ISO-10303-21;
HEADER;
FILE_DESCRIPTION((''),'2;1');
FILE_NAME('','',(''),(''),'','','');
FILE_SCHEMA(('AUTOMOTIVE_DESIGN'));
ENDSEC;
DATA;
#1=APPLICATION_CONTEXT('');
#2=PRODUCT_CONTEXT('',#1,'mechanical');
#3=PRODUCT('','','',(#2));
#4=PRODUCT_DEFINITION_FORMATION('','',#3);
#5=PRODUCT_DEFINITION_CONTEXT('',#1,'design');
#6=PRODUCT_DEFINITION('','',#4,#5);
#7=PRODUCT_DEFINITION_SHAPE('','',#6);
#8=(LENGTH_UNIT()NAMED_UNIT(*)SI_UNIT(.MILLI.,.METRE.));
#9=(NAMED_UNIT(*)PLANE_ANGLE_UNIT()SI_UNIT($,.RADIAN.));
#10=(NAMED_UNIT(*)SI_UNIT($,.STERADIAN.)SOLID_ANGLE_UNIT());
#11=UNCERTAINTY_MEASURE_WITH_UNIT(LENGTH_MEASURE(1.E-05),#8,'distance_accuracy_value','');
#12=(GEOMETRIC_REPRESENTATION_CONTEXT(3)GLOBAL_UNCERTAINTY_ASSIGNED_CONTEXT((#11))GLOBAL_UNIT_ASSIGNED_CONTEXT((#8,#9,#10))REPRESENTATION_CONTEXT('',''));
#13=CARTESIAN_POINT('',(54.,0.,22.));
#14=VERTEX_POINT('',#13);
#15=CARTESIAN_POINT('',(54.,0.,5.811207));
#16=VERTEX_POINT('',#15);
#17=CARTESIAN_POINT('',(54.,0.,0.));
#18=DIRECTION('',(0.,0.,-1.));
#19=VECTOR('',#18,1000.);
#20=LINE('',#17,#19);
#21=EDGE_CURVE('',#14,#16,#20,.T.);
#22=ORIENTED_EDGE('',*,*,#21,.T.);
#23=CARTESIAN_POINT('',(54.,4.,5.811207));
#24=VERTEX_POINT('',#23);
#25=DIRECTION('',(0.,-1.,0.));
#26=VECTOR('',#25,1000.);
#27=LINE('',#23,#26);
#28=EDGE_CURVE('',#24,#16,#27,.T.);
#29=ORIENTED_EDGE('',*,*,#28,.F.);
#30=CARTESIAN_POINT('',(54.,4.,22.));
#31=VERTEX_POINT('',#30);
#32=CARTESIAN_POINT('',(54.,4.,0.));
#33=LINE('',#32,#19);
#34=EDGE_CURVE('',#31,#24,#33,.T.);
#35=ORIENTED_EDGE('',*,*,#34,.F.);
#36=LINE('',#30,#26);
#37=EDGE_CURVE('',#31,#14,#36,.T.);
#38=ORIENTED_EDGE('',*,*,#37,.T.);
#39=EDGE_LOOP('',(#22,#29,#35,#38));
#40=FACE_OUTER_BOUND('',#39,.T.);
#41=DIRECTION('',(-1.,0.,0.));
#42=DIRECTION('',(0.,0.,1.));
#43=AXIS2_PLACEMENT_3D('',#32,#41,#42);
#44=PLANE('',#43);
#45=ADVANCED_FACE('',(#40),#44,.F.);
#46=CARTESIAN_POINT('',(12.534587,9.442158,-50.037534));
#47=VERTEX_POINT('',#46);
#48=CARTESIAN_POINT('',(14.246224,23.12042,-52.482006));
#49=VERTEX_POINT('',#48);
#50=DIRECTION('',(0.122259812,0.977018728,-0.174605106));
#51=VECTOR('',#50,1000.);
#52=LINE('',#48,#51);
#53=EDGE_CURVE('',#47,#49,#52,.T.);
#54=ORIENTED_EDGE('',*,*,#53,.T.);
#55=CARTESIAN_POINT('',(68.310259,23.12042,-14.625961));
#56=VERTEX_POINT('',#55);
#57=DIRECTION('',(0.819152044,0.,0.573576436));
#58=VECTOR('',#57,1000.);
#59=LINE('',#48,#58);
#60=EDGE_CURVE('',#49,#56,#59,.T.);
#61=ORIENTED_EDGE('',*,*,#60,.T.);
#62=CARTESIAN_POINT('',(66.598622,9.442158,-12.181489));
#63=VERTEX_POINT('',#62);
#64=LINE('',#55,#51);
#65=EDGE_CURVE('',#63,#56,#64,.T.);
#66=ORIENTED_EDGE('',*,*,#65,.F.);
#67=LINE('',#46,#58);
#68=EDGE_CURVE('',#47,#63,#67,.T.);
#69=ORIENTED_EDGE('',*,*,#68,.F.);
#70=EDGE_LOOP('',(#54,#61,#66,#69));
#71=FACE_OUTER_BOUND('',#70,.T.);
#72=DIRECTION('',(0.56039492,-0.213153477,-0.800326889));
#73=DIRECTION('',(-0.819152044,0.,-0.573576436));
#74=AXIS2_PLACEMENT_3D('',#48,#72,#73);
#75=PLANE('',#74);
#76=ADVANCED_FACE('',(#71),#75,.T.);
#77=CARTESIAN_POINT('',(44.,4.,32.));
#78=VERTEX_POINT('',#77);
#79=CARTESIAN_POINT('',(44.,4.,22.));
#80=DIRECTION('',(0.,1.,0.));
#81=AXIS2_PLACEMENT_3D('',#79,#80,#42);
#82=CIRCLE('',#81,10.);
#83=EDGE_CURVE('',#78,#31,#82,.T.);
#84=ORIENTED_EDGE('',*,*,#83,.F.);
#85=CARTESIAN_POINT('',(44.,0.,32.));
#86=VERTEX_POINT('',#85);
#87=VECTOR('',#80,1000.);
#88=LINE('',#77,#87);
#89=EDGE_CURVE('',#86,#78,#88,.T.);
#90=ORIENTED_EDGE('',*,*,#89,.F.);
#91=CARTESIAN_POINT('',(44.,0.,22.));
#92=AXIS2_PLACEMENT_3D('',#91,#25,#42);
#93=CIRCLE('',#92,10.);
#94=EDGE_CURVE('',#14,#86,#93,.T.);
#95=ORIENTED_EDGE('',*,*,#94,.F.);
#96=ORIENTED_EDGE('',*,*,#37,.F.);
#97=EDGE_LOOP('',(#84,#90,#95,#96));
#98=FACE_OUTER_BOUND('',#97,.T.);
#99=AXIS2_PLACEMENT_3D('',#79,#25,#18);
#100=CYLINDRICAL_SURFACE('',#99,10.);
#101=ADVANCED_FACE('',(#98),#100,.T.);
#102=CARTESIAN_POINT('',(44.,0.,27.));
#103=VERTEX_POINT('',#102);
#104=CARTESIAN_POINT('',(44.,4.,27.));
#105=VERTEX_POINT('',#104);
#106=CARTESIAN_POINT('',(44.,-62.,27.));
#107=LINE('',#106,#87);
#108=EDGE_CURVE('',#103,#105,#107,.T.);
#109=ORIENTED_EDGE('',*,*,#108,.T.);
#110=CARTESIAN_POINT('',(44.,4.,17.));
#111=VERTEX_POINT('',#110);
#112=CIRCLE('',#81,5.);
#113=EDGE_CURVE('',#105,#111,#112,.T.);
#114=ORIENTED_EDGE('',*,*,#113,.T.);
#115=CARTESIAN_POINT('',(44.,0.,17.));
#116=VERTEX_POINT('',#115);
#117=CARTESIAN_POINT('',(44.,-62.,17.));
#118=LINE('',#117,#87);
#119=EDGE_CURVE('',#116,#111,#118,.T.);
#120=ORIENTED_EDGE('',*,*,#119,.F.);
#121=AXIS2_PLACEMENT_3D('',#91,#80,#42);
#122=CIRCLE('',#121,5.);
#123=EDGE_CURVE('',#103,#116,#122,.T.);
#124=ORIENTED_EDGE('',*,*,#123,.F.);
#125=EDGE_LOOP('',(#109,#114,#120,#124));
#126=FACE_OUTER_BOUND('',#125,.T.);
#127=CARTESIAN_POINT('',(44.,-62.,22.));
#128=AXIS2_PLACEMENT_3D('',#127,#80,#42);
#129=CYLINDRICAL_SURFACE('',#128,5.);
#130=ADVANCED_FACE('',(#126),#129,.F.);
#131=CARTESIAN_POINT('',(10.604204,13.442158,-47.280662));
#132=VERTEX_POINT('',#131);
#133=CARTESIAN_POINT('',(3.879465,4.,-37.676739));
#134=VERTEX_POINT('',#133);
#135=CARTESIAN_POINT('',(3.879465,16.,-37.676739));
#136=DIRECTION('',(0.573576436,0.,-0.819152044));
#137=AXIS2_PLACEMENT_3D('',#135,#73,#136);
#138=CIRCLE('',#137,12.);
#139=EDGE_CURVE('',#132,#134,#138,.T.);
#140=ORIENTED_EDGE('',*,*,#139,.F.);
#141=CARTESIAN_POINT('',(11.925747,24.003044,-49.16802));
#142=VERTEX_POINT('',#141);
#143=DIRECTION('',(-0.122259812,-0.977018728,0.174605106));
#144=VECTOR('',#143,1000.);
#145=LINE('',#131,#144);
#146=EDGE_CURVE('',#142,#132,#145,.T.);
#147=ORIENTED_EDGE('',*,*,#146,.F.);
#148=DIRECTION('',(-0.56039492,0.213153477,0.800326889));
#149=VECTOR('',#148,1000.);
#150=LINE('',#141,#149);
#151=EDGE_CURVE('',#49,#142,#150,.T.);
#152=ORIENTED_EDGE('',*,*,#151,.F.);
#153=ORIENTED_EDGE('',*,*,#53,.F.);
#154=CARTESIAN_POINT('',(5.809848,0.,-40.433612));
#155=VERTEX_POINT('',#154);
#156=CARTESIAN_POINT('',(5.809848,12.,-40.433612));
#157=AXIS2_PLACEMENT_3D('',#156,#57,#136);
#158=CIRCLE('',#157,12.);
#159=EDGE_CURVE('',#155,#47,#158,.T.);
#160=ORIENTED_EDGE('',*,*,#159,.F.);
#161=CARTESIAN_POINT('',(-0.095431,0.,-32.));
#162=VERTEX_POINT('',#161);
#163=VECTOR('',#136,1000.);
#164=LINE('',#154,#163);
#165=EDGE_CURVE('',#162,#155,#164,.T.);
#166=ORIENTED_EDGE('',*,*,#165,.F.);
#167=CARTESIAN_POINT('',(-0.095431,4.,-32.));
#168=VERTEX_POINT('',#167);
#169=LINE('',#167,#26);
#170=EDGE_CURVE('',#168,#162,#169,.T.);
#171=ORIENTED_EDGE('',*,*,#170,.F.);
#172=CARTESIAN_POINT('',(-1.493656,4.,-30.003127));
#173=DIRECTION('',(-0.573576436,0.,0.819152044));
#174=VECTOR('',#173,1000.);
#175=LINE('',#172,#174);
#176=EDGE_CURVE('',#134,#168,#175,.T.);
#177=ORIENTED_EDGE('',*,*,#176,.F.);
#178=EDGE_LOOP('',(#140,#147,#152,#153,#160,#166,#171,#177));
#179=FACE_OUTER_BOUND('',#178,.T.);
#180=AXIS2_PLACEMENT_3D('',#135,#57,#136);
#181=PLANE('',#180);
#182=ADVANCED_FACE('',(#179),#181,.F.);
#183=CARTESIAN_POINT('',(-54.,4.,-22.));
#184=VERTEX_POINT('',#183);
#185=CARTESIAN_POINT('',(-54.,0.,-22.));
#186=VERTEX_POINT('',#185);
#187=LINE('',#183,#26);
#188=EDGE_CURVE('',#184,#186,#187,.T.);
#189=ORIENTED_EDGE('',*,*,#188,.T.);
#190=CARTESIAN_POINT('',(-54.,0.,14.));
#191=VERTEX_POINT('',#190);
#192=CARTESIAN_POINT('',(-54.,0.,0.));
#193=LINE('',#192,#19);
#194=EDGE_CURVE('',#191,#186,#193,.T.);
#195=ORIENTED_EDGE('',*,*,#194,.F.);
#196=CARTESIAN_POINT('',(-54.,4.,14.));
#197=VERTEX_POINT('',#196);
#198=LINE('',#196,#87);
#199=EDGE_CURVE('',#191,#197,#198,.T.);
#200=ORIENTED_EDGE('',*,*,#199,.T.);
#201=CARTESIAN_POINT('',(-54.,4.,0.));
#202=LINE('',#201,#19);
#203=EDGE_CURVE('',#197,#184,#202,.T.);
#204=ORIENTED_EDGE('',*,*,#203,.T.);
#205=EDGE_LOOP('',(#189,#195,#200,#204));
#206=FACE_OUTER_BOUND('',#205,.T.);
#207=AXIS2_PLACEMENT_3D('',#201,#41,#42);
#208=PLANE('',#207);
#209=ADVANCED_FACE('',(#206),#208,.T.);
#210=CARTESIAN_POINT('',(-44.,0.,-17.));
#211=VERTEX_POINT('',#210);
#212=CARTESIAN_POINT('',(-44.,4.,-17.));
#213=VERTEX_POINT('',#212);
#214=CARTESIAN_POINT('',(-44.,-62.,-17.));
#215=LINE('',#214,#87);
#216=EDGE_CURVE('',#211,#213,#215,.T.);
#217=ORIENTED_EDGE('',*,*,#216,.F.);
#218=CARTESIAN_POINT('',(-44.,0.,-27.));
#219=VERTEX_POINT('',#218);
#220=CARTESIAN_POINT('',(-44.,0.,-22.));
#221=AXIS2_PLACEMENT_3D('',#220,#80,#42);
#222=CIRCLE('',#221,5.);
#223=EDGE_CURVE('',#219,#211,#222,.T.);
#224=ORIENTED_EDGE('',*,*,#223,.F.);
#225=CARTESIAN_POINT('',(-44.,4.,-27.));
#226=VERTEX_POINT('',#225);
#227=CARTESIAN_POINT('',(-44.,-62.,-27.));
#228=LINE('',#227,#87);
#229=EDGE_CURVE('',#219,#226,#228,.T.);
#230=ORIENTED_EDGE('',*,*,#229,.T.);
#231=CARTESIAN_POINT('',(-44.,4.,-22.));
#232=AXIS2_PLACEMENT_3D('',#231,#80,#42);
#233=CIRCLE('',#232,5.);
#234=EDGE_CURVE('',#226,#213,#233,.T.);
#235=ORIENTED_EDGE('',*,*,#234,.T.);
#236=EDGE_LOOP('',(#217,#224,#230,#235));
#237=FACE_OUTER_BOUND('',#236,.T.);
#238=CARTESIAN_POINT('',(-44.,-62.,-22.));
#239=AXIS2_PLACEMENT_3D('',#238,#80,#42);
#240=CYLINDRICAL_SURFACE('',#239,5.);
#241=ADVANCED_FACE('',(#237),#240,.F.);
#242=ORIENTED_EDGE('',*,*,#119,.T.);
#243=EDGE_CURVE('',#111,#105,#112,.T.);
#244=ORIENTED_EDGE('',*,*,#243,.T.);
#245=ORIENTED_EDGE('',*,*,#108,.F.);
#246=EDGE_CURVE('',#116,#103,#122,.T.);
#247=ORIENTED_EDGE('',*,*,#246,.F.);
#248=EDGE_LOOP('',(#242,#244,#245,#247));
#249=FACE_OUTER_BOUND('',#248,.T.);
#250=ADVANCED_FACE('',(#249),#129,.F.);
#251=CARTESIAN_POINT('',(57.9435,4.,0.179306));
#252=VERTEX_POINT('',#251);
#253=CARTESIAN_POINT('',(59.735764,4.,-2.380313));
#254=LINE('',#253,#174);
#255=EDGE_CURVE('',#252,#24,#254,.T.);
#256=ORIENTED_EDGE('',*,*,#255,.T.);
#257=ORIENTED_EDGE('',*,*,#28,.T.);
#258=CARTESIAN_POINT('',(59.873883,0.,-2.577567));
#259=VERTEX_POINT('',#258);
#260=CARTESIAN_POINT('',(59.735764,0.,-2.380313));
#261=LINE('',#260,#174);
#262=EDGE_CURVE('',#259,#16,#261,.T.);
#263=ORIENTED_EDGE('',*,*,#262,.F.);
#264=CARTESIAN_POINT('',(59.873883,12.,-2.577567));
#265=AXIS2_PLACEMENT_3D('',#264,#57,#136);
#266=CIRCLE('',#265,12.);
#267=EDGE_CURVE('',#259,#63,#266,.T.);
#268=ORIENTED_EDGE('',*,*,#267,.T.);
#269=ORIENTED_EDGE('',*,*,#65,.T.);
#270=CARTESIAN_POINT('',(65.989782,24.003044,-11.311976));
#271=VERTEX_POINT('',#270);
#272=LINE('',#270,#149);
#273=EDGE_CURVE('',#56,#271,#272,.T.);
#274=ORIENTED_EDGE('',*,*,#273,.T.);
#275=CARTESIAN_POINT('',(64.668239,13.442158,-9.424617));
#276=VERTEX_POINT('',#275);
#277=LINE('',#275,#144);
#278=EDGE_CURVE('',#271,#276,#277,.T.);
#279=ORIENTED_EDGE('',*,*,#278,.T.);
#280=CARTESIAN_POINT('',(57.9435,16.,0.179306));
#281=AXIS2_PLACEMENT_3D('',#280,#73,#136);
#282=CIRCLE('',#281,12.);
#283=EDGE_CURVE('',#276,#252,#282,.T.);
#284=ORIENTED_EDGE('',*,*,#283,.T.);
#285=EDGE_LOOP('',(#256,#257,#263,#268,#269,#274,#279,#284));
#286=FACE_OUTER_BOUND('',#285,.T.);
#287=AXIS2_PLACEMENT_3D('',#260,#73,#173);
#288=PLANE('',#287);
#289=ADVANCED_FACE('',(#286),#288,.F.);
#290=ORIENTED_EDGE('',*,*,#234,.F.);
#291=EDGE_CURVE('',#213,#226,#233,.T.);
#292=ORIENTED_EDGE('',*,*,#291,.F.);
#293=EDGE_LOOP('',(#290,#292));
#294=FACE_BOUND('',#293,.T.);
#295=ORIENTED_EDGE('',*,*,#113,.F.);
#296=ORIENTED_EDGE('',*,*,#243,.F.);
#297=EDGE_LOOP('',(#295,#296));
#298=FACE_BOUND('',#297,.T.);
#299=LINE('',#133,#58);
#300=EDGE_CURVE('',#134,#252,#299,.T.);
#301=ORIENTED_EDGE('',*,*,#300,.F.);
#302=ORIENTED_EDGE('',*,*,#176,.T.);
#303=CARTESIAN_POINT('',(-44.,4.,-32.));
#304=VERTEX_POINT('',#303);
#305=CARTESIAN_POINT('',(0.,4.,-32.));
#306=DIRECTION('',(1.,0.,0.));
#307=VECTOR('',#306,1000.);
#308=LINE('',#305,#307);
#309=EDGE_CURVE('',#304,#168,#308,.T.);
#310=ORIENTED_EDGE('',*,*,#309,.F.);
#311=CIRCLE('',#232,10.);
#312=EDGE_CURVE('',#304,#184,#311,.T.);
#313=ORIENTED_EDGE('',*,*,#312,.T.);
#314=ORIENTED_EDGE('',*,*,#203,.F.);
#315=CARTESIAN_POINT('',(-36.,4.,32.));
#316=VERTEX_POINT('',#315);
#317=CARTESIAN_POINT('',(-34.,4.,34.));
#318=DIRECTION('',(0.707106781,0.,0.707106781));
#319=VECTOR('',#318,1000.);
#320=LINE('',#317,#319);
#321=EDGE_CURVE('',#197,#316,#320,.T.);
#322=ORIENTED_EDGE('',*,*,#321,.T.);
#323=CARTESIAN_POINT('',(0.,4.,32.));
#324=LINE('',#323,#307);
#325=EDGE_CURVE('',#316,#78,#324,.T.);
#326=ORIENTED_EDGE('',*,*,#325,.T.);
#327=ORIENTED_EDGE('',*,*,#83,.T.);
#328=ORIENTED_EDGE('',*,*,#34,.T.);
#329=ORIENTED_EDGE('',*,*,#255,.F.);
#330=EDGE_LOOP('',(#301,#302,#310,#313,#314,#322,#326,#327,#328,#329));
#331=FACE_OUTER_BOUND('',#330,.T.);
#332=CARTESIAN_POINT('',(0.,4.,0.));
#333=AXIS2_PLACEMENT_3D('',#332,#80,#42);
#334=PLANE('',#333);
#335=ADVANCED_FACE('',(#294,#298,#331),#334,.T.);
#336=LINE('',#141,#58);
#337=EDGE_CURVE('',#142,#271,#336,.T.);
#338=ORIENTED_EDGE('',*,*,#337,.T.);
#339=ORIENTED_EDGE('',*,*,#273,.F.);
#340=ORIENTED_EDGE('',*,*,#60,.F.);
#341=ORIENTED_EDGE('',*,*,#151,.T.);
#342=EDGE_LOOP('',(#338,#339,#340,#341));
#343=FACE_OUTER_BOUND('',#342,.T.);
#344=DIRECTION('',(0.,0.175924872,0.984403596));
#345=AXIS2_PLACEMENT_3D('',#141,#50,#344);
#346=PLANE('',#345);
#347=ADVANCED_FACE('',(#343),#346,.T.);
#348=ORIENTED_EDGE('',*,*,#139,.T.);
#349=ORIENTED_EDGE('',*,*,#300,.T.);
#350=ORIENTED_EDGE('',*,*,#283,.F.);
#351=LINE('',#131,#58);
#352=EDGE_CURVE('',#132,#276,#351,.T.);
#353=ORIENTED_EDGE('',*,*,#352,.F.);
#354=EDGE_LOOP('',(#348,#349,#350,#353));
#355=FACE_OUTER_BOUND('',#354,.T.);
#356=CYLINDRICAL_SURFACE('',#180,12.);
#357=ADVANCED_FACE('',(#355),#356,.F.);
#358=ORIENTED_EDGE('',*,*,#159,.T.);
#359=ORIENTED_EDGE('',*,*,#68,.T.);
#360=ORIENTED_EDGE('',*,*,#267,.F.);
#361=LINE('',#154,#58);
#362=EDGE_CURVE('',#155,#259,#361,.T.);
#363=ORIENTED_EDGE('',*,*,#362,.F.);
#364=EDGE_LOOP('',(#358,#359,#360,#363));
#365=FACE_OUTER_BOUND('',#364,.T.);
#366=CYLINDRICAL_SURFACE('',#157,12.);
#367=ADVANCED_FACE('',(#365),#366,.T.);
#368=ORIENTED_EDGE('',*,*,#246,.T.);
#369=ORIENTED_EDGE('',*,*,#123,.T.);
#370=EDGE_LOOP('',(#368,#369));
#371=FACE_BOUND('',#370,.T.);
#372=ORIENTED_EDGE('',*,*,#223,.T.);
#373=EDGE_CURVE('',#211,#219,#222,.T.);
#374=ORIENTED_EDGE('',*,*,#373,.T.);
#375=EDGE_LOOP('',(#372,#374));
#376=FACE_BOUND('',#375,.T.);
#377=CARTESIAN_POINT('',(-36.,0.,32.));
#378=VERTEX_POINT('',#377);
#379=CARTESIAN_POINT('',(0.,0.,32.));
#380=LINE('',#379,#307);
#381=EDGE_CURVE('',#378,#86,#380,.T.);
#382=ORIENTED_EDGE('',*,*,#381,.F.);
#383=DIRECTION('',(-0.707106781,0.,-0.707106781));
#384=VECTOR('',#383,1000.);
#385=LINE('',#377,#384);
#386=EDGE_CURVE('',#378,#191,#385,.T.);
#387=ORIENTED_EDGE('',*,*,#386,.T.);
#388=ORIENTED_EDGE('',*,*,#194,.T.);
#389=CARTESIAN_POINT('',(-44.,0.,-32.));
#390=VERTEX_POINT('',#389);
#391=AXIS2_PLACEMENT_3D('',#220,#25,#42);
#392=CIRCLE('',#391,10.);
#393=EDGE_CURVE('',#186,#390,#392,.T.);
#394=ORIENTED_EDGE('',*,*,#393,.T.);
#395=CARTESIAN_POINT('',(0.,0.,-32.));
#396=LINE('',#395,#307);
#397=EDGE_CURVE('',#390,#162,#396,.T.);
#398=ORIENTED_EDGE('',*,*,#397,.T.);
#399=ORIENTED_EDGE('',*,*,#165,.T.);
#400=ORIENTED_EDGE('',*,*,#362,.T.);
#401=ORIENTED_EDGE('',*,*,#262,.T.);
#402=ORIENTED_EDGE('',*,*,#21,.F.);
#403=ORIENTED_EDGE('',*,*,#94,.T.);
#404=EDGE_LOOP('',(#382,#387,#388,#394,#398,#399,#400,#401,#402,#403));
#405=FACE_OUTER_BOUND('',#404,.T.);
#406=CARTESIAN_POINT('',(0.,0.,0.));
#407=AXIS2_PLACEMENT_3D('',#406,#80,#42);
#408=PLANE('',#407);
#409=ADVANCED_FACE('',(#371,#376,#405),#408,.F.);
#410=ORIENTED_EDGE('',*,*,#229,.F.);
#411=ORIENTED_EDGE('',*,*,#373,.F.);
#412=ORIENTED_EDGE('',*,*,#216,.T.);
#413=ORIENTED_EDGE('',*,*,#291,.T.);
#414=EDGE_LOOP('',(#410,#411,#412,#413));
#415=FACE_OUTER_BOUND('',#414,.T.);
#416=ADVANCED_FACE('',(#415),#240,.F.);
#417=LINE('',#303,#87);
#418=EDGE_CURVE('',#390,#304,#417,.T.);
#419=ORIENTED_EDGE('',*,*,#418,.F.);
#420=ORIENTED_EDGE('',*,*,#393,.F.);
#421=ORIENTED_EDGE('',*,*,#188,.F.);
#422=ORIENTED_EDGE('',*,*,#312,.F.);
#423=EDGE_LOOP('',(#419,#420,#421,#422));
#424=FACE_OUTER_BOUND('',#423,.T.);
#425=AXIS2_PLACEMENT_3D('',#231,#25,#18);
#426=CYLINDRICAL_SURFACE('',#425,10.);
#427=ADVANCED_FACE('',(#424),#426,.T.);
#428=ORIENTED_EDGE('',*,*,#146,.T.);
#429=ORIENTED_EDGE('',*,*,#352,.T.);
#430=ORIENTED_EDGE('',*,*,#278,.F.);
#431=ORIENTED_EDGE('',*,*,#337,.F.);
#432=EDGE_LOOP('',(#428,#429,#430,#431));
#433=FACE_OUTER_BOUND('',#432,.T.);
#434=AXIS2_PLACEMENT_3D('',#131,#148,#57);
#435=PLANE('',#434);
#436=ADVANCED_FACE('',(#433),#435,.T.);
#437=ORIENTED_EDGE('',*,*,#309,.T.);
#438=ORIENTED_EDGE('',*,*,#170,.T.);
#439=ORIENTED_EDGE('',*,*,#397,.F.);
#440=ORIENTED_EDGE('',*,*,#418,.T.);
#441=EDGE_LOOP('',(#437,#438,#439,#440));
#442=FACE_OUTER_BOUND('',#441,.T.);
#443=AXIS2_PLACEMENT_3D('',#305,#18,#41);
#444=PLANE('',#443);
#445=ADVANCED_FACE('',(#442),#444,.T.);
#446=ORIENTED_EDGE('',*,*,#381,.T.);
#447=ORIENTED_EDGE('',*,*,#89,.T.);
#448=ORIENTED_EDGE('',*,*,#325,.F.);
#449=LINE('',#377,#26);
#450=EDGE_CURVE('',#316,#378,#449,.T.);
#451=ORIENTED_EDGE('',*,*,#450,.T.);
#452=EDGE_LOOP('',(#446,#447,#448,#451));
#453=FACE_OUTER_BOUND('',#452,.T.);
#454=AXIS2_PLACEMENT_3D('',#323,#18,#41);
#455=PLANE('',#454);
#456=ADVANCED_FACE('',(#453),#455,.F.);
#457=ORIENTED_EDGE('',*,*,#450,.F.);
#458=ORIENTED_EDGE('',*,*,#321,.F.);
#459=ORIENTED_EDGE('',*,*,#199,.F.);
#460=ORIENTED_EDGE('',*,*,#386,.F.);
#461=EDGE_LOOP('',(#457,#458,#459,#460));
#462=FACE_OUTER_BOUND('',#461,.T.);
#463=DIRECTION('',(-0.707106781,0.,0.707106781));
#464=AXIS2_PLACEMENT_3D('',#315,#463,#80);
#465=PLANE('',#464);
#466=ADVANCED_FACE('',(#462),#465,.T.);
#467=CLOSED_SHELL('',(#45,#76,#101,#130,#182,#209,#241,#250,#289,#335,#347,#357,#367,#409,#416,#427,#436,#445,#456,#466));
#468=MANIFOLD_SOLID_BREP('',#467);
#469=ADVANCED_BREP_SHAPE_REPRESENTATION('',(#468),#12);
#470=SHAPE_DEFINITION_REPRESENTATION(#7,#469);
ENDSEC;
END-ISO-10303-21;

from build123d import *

# Parameters (mm, degrees)
BASE_PLATE_DEPTH             = 4
FLANGE_RISER_SKETCH_W        = 65.921827793
FLANGE_RISER_SKETCH_H        = 4
FLANGE_RISER_DEPTH           = 10
CURVED_FLANGE_DEPTH          = 66
PLATE_CORNER_FILLETS_R10_R   = 10
PLATE_CORNER_CHAMFER_18_SIZE = 18
MOUNTING_HOLES_SKETCH_R      = 5
MOUNTING_HOLES_2X_DEPTH      = 66


with BuildPart() as part:
    # Base Plate Sketch → Base Plate (new body)
    with BuildSketch(Plane(origin=(0, 0, 0), x_dir=(1, 0, 0), z_dir=(0, 1, 0))):
        Polygon((-54, -32), (54, -32), (54, -5.811207063), (0, 32), (-54, 32), align=None)
    extrude(amount=BASE_PLATE_DEPTH)

    # Flange Riser Sketch → Flange Riser (add)
    with BuildSketch(Plane(origin=(15.035081933, 0, -21.472322293), x_dir=(-0.8191520442889909, 0, -0.5735764363510474), z_dir=(0.5735764363510474, 0, -0.8191520442889909))):
        with Locations((-14.606467934, 2)):
            Rectangle(FLANGE_RISER_SKETCH_W, FLANGE_RISER_SKETCH_H)
    extrude(amount=FLANGE_RISER_DEPTH)

    # Curved Flange Profile Sketch → Curved Flange (add)
    with BuildSketch(Plane(origin=(38.964918067, 0, 27.283529357), x_dir=(0.5735764363510477, 0, -0.8191520442889908), z_dir=(0.8191520442889907, 0, 0.5735764363510476))):
        with BuildLine():
            Line((23.720397301, 4), (33.088147536, 4))
            ThreePointArc((33.088147536, 4), (40.61496291, 6.654035613), (44.812372275, 13.442158279))
            Line((44.812372275, 13.442158279), (47.116411582, 24.003044212))
            Line((47.116411582, 24.003044212), (51.162040745, 23.120420475))
            Line((51.162040745, 23.120420475), (48.17789207, 9.442158279))
            ThreePointArc((48.17789207, 9.442158279), (43.980482705, 2.654035613), (36.453667331, 0))
            Line((36.453667331, 0), (24.245794341, 0))
            Line((24.245794341, 0), (23.720397301, 4))
        make_face()
    extrude(amount=-CURVED_FLANGE_DEPTH)

    # Plate Corner Fillets R10
    plate_corner_fillets_r10_edges = [part.edges().sort_by_distance(p)[0] for p in [
        (-54, 2, -32),
        (54, 2, 32),
    ]]
    fillet(plate_corner_fillets_r10_edges, radius=PLATE_CORNER_FILLETS_R10_R)

    # Plate Corner Chamfer 18
    plate_corner_chamfer_18_edges = [part.edges().sort_by_distance(p)[0] for p in [
        (-54, 2, 32),
    ]]
    chamfer(plate_corner_chamfer_18_edges, length=PLATE_CORNER_CHAMFER_18_SIZE)

    # Mounting Holes Sketch → Mounting Holes 2x (cut)
    with BuildSketch(Plane(origin=(0, 4, 0), x_dir=(1, 0, 0), z_dir=(0, 1, 0))):
        with Locations(Location((-44, 22, 0), (0, 0, 270))):
            Circle(MOUNTING_HOLES_SKETCH_R)
        with Locations(Location((44, -22, 0), (0, 0, 270))):
            Circle(MOUNTING_HOLES_SKETCH_R)
    extrude(amount=-MOUNTING_HOLES_2X_DEPTH, mode=Mode.SUBTRACT)


solid = part.part
